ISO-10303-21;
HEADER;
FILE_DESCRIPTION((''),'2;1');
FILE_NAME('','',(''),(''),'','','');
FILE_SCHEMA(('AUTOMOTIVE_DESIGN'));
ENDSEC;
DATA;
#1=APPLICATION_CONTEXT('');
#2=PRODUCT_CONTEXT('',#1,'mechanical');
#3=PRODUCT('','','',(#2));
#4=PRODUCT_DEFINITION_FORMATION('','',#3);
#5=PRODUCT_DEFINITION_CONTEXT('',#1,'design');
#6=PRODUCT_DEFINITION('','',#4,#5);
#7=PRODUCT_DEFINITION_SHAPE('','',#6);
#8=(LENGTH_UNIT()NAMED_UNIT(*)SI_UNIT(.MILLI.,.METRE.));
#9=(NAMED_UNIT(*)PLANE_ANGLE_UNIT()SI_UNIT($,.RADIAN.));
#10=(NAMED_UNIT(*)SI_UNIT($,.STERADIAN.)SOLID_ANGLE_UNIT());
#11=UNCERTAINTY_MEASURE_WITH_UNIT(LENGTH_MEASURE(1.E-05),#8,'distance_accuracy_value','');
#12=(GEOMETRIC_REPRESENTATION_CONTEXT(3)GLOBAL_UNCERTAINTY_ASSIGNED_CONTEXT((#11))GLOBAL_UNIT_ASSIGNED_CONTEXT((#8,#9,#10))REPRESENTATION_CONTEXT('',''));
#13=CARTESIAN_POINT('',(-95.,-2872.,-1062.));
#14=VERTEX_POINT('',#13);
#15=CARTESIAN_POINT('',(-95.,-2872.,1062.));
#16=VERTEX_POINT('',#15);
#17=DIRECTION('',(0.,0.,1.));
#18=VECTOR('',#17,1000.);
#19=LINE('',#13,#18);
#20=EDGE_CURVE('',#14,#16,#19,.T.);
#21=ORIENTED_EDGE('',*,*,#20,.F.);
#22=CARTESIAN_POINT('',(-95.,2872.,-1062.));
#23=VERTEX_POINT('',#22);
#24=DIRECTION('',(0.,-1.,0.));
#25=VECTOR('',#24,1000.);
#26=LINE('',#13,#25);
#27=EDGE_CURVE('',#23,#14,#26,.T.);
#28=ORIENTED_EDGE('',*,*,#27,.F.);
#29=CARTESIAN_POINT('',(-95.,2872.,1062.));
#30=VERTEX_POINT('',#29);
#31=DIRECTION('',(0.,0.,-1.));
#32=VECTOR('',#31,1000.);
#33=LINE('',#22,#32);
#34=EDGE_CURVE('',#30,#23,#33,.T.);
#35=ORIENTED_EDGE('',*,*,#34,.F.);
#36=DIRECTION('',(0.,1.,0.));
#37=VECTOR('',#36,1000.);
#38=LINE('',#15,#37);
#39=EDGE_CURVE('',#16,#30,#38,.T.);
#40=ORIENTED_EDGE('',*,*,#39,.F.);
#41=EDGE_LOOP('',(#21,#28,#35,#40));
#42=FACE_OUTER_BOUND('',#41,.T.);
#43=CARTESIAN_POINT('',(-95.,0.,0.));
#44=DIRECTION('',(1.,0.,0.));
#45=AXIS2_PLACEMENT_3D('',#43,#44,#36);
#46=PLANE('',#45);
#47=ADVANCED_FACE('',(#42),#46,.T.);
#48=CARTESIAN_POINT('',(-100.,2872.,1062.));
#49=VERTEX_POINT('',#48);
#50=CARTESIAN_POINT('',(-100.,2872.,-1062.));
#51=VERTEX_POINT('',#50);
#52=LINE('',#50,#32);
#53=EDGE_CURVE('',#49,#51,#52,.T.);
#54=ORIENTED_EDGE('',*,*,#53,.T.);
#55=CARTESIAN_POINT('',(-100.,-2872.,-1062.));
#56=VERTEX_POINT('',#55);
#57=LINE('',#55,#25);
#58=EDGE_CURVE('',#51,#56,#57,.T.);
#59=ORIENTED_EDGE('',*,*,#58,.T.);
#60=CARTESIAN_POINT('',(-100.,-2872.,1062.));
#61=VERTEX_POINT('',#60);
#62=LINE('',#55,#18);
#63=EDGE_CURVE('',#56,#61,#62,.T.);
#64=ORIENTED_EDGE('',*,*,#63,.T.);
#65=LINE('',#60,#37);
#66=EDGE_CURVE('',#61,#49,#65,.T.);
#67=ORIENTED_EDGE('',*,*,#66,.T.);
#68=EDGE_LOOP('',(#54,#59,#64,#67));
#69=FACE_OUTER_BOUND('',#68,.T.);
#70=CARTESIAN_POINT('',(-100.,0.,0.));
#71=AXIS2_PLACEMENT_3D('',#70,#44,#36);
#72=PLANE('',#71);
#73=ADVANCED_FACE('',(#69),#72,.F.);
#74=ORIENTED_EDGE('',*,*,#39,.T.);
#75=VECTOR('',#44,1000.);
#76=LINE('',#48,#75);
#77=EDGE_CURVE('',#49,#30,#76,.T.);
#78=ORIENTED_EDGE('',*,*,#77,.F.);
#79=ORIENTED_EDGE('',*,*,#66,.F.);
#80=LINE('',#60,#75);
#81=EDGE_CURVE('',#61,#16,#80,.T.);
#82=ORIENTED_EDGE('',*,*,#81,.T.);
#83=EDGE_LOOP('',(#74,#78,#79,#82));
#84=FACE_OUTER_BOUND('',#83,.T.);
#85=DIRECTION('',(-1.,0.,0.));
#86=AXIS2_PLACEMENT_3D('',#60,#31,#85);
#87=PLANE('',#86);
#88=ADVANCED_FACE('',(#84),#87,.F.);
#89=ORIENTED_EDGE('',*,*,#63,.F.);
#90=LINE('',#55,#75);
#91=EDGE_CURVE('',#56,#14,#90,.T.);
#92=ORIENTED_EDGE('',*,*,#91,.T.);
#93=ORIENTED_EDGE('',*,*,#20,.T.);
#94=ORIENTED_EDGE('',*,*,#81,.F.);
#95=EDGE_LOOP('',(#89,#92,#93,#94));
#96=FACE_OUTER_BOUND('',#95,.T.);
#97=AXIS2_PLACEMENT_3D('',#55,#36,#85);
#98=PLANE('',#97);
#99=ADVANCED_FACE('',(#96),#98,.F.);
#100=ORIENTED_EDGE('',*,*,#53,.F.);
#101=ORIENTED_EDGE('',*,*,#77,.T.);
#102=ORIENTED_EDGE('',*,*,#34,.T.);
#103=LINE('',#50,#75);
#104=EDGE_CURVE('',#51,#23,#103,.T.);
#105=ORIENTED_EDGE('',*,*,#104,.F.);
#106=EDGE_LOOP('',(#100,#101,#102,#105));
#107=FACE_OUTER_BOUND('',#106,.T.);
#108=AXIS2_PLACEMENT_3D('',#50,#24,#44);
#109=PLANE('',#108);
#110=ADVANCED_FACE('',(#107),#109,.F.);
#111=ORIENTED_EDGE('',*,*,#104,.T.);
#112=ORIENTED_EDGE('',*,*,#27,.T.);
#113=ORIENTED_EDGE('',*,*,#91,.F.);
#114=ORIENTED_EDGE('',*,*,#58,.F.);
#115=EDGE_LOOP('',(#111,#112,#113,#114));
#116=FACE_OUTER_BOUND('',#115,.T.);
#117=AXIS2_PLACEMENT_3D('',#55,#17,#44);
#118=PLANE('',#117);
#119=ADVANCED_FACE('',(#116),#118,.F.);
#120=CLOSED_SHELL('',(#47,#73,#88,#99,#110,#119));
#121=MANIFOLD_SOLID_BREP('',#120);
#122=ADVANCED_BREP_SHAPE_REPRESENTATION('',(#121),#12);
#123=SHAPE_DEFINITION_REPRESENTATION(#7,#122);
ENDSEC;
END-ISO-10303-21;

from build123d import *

# Parameters (mm, degrees)
SKETCH1_W           = 2124
SKETCH1_H           = 5744
BOSS_EXTRUDE1_DEPTH = 5


with BuildPart() as part:
    # Sketch1 → Boss-Extrude1 (new body)
    with BuildSketch(Plane.ZY.offset(95)):
        Rectangle(SKETCH1_W, SKETCH1_H)
    extrude(amount=BOSS_EXTRUDE1_DEPTH)


solid = part.part
